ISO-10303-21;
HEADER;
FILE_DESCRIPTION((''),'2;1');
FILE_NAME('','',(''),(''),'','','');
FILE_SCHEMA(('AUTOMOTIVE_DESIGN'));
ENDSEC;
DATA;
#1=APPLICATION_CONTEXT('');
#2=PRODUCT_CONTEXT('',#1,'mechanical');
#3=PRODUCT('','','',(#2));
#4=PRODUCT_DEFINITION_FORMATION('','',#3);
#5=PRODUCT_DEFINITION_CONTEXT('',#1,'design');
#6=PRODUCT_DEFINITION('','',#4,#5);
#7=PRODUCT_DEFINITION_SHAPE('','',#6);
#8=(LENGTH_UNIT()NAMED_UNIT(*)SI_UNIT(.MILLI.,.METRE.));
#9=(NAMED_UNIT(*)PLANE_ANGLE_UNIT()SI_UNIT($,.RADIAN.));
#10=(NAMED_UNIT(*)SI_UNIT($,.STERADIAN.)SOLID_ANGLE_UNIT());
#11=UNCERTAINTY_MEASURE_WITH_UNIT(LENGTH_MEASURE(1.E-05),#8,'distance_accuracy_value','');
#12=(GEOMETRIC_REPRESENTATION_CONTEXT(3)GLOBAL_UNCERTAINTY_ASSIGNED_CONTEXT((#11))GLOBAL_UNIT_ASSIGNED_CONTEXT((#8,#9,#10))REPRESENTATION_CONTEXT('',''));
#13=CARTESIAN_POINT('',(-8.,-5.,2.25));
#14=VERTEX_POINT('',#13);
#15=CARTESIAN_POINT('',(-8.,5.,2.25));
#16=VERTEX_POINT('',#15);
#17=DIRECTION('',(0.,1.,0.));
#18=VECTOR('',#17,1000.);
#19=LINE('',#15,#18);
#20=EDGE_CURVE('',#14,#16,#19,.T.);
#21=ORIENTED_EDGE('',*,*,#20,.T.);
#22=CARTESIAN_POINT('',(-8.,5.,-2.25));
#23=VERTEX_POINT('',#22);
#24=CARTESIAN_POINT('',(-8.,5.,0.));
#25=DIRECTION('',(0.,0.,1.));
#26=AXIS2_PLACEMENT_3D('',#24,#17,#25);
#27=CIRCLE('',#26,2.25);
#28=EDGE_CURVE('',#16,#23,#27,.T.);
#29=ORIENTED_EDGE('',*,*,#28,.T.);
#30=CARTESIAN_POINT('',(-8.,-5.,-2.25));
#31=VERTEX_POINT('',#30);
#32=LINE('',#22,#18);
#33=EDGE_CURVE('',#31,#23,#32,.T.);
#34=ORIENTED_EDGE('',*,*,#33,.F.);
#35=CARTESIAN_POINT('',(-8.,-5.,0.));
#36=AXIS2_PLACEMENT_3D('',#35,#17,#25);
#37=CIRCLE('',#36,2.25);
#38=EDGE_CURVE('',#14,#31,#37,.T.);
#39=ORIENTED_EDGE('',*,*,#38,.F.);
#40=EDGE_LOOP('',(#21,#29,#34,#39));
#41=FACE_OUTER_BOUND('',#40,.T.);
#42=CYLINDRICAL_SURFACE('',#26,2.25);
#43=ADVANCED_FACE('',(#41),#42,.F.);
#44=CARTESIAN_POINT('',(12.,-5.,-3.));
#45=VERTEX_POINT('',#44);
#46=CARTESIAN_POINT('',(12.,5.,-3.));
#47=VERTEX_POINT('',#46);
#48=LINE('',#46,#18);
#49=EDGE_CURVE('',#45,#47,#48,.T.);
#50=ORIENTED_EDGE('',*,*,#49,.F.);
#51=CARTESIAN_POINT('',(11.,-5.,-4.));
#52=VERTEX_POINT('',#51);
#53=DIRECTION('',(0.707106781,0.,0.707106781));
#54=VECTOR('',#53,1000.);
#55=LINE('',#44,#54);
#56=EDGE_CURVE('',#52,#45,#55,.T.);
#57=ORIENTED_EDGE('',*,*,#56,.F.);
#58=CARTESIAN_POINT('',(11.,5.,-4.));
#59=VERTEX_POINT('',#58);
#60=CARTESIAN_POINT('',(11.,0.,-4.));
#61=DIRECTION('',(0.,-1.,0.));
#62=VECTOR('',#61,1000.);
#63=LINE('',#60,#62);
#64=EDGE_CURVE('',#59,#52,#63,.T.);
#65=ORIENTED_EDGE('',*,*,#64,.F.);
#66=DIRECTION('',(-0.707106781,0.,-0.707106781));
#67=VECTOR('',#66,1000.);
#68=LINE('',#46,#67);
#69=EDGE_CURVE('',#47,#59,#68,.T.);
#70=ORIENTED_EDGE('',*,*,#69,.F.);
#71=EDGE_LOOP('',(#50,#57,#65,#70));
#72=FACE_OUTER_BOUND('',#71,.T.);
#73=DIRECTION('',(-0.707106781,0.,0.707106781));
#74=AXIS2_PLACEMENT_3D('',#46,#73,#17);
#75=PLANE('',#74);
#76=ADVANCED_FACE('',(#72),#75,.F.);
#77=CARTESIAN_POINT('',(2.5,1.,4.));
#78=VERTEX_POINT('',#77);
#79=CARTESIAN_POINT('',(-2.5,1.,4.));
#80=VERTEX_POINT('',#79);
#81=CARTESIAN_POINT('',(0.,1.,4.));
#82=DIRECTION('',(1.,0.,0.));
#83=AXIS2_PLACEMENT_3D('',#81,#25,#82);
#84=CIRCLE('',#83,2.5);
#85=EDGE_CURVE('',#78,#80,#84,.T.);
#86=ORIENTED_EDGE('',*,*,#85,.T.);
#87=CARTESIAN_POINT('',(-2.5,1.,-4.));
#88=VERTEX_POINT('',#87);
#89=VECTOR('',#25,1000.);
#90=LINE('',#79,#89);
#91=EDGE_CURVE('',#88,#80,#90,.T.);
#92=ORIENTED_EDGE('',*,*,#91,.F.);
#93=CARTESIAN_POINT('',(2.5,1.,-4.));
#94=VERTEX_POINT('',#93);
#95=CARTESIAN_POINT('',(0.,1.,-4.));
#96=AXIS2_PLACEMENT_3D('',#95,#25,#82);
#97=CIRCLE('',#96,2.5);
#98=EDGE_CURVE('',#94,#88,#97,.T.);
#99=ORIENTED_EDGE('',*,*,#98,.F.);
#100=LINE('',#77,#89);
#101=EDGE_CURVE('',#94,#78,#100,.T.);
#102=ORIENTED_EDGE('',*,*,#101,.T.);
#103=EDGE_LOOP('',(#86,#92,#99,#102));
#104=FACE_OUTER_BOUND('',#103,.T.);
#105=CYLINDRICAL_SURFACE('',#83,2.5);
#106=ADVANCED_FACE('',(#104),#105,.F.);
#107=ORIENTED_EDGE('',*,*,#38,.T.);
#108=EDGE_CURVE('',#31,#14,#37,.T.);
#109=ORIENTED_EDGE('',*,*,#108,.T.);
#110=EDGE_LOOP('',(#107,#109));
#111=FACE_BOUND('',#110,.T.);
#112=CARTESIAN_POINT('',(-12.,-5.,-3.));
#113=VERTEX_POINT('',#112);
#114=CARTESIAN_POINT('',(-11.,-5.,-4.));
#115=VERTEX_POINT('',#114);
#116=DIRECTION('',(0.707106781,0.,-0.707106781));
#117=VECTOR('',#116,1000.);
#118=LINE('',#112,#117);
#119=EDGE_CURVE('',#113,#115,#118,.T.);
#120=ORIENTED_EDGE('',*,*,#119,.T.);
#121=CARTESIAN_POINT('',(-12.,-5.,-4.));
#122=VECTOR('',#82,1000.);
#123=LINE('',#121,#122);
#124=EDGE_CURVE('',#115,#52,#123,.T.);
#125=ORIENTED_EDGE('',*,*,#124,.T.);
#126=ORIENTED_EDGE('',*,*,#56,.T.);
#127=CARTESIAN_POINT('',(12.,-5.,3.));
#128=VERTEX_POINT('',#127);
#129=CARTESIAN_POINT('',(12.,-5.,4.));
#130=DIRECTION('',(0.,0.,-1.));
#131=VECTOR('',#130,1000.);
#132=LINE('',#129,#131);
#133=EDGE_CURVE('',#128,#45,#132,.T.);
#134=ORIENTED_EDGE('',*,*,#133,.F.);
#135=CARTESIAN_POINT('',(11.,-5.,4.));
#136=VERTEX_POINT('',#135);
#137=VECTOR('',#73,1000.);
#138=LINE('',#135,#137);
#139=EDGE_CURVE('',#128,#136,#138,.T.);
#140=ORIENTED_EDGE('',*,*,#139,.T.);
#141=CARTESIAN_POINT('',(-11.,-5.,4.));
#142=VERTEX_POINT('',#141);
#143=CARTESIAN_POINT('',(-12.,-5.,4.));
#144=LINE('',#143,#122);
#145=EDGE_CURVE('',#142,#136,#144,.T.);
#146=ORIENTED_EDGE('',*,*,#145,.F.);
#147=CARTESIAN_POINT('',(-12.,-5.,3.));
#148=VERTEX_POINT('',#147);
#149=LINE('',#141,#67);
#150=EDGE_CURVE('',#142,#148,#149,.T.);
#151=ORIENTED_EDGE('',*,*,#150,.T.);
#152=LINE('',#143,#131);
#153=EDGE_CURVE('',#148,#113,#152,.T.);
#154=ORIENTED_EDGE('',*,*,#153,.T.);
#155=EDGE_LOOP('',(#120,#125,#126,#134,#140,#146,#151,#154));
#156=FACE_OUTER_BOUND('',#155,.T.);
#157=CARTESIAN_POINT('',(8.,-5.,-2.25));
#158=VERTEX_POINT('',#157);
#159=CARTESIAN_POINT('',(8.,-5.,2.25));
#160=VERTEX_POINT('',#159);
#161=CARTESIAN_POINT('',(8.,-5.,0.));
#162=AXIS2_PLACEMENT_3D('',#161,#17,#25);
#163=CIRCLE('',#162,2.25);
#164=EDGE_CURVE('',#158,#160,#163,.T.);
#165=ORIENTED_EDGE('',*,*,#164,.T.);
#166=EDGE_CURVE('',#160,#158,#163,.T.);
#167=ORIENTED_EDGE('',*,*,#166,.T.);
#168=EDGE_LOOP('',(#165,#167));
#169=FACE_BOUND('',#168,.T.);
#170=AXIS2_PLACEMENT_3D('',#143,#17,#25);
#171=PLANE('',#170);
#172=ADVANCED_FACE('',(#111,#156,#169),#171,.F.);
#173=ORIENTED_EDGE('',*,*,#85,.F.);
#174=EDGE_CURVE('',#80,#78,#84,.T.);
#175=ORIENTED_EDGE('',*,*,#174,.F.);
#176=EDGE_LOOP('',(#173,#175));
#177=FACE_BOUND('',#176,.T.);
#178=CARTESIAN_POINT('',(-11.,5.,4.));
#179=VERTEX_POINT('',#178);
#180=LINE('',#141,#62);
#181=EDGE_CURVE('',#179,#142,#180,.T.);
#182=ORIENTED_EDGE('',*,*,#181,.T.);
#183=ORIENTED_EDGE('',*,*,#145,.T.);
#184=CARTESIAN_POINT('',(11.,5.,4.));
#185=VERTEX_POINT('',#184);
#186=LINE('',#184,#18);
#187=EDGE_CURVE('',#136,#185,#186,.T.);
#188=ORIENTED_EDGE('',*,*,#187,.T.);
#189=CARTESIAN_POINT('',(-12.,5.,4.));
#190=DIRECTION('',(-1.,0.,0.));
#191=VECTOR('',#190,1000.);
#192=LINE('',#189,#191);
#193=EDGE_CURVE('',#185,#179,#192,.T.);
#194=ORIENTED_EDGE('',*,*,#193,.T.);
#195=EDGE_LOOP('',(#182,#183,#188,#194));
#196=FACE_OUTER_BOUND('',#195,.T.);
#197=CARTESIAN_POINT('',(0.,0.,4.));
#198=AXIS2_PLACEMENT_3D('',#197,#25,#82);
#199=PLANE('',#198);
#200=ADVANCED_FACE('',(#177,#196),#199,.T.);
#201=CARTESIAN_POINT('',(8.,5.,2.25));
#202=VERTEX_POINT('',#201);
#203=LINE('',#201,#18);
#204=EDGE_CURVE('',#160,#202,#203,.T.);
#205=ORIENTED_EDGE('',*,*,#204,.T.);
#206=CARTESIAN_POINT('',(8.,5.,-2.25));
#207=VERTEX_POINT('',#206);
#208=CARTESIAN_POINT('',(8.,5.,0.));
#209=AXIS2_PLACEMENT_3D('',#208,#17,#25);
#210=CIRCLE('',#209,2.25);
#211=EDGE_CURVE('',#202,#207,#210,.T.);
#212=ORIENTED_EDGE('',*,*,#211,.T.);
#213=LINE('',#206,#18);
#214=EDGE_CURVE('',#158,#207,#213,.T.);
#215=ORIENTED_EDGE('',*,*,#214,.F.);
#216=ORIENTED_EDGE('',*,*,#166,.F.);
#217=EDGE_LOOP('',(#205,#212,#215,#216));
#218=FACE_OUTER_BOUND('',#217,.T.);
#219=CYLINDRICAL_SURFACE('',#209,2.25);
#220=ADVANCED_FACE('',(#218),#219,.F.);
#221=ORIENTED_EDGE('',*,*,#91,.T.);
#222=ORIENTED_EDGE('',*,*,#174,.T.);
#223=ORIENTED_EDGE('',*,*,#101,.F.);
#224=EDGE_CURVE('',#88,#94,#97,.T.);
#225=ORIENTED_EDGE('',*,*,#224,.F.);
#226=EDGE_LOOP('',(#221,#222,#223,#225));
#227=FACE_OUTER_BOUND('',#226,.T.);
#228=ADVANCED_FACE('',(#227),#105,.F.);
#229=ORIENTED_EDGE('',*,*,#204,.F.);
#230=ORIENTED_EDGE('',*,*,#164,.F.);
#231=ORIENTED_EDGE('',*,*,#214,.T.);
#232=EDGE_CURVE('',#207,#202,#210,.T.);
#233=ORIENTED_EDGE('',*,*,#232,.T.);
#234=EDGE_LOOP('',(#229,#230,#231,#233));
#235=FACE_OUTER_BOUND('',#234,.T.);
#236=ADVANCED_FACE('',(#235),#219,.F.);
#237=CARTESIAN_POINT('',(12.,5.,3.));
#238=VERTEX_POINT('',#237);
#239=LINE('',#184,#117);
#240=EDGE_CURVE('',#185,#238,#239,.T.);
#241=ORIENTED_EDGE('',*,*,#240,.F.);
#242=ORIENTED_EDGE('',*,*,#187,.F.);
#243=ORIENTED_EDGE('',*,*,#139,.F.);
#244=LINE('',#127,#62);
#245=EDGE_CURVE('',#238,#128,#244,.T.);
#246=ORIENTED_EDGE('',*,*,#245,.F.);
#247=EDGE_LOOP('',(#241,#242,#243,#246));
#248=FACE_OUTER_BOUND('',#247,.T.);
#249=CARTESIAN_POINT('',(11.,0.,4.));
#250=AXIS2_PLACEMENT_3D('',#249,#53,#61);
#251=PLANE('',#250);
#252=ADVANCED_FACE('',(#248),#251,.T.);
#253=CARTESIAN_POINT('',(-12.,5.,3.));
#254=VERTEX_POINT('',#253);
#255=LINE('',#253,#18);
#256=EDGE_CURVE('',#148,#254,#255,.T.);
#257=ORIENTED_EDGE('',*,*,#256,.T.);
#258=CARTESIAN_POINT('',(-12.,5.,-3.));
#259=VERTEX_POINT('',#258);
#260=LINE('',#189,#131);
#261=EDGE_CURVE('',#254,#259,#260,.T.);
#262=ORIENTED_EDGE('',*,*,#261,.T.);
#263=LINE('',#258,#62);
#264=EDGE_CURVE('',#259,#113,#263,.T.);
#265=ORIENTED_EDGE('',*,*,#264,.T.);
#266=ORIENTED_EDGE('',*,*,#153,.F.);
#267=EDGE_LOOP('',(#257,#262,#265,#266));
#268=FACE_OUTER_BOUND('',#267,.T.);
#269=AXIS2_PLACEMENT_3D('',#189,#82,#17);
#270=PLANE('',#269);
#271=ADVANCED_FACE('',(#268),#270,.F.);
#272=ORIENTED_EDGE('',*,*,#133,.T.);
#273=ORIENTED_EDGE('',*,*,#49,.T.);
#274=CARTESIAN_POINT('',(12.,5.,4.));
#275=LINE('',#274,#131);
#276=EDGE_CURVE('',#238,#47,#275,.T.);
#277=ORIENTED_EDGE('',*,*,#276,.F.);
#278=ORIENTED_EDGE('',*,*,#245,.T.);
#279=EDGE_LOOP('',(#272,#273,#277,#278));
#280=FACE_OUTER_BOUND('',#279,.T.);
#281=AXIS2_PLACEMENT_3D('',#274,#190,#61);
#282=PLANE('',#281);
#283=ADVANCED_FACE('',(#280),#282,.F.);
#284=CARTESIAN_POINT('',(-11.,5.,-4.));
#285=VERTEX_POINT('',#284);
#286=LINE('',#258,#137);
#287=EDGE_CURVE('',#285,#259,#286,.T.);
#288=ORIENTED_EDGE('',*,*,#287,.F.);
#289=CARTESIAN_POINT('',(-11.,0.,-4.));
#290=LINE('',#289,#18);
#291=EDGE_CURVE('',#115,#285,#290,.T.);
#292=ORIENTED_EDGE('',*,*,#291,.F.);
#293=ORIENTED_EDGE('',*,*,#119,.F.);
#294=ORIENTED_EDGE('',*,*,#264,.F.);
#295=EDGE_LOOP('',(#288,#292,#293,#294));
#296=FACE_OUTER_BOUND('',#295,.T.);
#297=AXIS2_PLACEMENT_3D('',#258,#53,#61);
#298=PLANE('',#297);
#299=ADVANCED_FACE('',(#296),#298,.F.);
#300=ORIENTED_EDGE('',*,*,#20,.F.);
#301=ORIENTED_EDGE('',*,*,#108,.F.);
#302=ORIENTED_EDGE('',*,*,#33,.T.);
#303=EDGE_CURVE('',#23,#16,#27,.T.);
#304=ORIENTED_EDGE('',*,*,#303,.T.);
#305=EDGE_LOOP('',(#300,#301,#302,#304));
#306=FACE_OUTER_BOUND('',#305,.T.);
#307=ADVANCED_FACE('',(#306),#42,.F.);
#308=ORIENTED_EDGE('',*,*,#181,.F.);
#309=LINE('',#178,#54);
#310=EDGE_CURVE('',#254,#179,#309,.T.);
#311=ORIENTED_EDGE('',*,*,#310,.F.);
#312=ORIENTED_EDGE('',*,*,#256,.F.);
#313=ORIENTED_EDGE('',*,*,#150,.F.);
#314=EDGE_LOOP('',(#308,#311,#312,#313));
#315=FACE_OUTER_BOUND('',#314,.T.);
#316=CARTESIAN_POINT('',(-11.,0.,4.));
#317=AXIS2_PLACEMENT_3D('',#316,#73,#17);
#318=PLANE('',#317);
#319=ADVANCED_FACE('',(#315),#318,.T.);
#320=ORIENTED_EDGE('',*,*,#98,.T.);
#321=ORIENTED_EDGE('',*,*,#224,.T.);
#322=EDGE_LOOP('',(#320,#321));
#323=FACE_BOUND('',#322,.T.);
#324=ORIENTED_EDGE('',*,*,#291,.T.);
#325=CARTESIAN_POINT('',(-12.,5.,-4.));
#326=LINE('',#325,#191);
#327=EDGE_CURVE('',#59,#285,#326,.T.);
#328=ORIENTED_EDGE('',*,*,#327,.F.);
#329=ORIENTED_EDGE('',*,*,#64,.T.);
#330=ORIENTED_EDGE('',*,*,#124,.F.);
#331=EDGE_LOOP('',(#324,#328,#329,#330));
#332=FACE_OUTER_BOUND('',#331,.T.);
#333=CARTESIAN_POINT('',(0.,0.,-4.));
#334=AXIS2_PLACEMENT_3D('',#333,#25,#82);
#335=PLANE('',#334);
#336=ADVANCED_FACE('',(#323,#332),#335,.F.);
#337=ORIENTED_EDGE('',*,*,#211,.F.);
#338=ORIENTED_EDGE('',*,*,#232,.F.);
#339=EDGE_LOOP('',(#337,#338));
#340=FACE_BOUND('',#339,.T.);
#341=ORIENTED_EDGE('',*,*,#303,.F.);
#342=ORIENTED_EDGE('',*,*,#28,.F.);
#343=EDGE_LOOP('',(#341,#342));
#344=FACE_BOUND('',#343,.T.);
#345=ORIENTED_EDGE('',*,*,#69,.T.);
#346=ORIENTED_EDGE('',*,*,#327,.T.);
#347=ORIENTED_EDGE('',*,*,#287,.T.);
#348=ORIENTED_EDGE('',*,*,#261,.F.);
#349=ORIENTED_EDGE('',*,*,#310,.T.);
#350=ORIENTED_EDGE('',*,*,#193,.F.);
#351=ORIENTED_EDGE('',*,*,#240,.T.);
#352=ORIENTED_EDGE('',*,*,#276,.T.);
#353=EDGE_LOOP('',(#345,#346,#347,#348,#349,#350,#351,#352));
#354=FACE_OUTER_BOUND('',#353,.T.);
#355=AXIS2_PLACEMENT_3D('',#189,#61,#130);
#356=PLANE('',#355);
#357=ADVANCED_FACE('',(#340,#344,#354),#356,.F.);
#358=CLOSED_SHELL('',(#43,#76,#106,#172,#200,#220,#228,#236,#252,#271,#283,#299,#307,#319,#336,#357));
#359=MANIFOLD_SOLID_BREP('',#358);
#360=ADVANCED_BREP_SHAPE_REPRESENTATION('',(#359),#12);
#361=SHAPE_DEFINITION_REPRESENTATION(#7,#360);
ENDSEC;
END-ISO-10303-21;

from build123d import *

# Parameters (mm, degrees)
SKETCH1_W                  = 24
SKETCH1_H                  = 10
BOSS_EXTRUDE1_DEPTH        = 4
F_4_5_4_5_DIAMETER_HOLE1_D = 4.5
CHAMFER1_SIZE              = 1
F_5_0_5_DIAMETER_HOLE1_D   = 5


with BuildPart() as part:
    # Sketch1 → Boss-Extrude1 (new, symmetric)
    with BuildSketch(Plane.XY):
        Rectangle(SKETCH1_W, SKETCH1_H)
    extrude(amount=BOSS_EXTRUDE1_DEPTH, both=True)

    # Ø4.5 (4.5) Diameter Hole1 (through all)
    with Locations(Plane(origin=(0, 5, 0), x_dir=(1, 0, 0), z_dir=(0, 1, 0))):
        with Locations((-8, 0), (8, 0)):
            Hole(F_4_5_4_5_DIAMETER_HOLE1_D / 2)

    # Chamfer1
    chamfer1_edges = [part.edges().sort_by_distance(p)[0] for p in [
        (-12, 0, 4),
        (12, 0, 4),
        (-12, 0, -4),
        (12, 0, -4),
    ]]
    chamfer(chamfer1_edges, length=CHAMFER1_SIZE)

    # Ø5.0 (5) Diameter Hole1 (through all)
    with Locations(Plane.XY.offset(4)):
        with Locations((0, 1)):
            Hole(F_5_0_5_DIAMETER_HOLE1_D / 2)


solid = part.part
